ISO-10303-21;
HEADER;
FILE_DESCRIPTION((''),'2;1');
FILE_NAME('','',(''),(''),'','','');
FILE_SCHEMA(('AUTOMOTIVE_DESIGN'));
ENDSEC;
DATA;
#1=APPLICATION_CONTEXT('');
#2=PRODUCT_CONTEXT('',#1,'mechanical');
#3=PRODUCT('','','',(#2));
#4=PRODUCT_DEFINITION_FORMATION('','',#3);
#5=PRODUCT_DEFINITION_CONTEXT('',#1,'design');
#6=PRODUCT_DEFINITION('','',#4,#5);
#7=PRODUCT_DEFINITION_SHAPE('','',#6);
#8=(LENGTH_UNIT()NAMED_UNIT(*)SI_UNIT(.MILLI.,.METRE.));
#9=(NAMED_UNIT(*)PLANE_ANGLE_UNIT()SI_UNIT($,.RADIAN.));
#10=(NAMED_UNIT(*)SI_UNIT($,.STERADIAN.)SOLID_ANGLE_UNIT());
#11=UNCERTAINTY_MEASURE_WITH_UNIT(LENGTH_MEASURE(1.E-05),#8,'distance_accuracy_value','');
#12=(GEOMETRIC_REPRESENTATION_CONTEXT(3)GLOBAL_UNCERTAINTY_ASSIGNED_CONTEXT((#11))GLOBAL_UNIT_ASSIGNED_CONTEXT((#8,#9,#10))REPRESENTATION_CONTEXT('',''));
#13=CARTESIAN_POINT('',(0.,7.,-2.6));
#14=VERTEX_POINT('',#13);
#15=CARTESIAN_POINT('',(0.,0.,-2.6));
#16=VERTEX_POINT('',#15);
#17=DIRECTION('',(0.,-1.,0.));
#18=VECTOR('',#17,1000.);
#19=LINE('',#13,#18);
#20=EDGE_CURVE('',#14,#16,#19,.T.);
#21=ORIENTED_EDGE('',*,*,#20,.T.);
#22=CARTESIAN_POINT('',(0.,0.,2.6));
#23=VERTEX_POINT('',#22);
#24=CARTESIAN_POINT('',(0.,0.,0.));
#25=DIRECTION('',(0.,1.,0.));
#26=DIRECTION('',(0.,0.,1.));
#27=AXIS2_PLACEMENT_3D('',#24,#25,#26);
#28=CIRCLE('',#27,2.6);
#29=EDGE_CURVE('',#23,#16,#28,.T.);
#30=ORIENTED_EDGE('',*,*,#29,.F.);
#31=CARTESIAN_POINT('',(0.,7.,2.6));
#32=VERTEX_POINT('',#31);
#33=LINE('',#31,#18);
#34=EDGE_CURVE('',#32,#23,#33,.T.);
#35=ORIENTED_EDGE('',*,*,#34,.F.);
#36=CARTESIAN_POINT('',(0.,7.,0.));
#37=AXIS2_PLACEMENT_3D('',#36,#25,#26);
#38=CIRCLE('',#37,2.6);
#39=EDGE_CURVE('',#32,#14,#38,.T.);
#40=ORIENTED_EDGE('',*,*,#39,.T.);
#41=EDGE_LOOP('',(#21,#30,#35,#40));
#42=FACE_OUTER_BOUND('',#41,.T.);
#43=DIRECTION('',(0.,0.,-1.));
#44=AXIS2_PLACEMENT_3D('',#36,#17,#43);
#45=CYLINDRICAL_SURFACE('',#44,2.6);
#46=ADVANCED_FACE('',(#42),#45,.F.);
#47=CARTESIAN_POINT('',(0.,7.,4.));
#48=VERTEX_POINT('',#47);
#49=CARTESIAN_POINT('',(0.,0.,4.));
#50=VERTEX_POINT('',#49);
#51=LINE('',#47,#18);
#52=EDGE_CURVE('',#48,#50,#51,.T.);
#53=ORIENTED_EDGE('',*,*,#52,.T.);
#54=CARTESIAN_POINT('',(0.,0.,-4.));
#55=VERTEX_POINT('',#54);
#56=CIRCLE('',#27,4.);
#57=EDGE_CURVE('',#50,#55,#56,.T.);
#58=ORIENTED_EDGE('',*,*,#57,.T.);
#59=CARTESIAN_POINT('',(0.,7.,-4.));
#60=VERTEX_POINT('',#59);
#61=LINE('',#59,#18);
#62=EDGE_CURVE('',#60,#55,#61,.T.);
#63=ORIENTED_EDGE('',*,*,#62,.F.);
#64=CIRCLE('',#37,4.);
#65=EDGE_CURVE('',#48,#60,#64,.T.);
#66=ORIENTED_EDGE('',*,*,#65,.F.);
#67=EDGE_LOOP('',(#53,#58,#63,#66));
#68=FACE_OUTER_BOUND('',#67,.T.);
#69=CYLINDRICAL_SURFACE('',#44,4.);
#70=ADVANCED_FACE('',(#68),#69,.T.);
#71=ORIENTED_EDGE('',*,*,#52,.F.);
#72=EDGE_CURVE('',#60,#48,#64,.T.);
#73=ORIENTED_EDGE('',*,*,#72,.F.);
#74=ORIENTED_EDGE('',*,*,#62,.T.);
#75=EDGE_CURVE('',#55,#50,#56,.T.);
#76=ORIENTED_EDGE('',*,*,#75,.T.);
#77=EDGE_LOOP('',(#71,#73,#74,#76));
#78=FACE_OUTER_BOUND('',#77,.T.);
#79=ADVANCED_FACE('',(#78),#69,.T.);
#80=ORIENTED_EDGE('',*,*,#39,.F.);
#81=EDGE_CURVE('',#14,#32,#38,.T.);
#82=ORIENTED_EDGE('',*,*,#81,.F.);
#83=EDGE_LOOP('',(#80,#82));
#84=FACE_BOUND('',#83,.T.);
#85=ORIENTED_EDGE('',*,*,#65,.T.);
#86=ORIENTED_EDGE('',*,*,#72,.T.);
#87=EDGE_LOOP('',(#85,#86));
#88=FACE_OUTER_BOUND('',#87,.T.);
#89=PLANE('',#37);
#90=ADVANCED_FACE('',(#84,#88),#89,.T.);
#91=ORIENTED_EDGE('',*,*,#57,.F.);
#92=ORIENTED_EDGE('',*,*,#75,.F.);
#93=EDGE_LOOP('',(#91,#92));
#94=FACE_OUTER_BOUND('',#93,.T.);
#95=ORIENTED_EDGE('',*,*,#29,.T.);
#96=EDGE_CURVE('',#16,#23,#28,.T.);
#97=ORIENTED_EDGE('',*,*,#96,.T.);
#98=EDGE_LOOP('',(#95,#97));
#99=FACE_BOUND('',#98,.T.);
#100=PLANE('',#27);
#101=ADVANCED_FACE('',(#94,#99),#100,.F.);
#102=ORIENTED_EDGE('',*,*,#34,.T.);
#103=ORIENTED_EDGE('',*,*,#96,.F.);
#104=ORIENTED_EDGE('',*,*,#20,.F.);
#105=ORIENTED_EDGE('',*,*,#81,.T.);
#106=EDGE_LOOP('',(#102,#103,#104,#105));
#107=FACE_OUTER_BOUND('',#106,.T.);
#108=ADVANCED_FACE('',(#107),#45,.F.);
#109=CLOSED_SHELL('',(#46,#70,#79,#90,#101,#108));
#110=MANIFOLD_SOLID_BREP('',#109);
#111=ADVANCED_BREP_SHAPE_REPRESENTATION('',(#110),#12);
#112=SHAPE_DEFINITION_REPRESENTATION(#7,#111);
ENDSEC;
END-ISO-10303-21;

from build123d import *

# Parameters (mm, degrees)
SKETCH1_R           = 4
SKETCH1_R_2         = 2.6
BOSS_EXTRUDE1_DEPTH = 7


with BuildPart() as part:
    # Sketch1 → Boss-Extrude1 (new body)
    with BuildSketch(Plane(origin=(0, 0, 0), x_dir=(1, 0, 0), z_dir=(0, 1, 0))):
        with Locations(Location((0, 0, 0), (0, 0, 270))):
            Circle(SKETCH1_R)
        with Locations(Location((0, 0, 0), (0, 0, 270))):
            Circle(SKETCH1_R_2, mode=Mode.SUBTRACT)
    extrude(amount=BOSS_EXTRUDE1_DEPTH)


solid = part.part
